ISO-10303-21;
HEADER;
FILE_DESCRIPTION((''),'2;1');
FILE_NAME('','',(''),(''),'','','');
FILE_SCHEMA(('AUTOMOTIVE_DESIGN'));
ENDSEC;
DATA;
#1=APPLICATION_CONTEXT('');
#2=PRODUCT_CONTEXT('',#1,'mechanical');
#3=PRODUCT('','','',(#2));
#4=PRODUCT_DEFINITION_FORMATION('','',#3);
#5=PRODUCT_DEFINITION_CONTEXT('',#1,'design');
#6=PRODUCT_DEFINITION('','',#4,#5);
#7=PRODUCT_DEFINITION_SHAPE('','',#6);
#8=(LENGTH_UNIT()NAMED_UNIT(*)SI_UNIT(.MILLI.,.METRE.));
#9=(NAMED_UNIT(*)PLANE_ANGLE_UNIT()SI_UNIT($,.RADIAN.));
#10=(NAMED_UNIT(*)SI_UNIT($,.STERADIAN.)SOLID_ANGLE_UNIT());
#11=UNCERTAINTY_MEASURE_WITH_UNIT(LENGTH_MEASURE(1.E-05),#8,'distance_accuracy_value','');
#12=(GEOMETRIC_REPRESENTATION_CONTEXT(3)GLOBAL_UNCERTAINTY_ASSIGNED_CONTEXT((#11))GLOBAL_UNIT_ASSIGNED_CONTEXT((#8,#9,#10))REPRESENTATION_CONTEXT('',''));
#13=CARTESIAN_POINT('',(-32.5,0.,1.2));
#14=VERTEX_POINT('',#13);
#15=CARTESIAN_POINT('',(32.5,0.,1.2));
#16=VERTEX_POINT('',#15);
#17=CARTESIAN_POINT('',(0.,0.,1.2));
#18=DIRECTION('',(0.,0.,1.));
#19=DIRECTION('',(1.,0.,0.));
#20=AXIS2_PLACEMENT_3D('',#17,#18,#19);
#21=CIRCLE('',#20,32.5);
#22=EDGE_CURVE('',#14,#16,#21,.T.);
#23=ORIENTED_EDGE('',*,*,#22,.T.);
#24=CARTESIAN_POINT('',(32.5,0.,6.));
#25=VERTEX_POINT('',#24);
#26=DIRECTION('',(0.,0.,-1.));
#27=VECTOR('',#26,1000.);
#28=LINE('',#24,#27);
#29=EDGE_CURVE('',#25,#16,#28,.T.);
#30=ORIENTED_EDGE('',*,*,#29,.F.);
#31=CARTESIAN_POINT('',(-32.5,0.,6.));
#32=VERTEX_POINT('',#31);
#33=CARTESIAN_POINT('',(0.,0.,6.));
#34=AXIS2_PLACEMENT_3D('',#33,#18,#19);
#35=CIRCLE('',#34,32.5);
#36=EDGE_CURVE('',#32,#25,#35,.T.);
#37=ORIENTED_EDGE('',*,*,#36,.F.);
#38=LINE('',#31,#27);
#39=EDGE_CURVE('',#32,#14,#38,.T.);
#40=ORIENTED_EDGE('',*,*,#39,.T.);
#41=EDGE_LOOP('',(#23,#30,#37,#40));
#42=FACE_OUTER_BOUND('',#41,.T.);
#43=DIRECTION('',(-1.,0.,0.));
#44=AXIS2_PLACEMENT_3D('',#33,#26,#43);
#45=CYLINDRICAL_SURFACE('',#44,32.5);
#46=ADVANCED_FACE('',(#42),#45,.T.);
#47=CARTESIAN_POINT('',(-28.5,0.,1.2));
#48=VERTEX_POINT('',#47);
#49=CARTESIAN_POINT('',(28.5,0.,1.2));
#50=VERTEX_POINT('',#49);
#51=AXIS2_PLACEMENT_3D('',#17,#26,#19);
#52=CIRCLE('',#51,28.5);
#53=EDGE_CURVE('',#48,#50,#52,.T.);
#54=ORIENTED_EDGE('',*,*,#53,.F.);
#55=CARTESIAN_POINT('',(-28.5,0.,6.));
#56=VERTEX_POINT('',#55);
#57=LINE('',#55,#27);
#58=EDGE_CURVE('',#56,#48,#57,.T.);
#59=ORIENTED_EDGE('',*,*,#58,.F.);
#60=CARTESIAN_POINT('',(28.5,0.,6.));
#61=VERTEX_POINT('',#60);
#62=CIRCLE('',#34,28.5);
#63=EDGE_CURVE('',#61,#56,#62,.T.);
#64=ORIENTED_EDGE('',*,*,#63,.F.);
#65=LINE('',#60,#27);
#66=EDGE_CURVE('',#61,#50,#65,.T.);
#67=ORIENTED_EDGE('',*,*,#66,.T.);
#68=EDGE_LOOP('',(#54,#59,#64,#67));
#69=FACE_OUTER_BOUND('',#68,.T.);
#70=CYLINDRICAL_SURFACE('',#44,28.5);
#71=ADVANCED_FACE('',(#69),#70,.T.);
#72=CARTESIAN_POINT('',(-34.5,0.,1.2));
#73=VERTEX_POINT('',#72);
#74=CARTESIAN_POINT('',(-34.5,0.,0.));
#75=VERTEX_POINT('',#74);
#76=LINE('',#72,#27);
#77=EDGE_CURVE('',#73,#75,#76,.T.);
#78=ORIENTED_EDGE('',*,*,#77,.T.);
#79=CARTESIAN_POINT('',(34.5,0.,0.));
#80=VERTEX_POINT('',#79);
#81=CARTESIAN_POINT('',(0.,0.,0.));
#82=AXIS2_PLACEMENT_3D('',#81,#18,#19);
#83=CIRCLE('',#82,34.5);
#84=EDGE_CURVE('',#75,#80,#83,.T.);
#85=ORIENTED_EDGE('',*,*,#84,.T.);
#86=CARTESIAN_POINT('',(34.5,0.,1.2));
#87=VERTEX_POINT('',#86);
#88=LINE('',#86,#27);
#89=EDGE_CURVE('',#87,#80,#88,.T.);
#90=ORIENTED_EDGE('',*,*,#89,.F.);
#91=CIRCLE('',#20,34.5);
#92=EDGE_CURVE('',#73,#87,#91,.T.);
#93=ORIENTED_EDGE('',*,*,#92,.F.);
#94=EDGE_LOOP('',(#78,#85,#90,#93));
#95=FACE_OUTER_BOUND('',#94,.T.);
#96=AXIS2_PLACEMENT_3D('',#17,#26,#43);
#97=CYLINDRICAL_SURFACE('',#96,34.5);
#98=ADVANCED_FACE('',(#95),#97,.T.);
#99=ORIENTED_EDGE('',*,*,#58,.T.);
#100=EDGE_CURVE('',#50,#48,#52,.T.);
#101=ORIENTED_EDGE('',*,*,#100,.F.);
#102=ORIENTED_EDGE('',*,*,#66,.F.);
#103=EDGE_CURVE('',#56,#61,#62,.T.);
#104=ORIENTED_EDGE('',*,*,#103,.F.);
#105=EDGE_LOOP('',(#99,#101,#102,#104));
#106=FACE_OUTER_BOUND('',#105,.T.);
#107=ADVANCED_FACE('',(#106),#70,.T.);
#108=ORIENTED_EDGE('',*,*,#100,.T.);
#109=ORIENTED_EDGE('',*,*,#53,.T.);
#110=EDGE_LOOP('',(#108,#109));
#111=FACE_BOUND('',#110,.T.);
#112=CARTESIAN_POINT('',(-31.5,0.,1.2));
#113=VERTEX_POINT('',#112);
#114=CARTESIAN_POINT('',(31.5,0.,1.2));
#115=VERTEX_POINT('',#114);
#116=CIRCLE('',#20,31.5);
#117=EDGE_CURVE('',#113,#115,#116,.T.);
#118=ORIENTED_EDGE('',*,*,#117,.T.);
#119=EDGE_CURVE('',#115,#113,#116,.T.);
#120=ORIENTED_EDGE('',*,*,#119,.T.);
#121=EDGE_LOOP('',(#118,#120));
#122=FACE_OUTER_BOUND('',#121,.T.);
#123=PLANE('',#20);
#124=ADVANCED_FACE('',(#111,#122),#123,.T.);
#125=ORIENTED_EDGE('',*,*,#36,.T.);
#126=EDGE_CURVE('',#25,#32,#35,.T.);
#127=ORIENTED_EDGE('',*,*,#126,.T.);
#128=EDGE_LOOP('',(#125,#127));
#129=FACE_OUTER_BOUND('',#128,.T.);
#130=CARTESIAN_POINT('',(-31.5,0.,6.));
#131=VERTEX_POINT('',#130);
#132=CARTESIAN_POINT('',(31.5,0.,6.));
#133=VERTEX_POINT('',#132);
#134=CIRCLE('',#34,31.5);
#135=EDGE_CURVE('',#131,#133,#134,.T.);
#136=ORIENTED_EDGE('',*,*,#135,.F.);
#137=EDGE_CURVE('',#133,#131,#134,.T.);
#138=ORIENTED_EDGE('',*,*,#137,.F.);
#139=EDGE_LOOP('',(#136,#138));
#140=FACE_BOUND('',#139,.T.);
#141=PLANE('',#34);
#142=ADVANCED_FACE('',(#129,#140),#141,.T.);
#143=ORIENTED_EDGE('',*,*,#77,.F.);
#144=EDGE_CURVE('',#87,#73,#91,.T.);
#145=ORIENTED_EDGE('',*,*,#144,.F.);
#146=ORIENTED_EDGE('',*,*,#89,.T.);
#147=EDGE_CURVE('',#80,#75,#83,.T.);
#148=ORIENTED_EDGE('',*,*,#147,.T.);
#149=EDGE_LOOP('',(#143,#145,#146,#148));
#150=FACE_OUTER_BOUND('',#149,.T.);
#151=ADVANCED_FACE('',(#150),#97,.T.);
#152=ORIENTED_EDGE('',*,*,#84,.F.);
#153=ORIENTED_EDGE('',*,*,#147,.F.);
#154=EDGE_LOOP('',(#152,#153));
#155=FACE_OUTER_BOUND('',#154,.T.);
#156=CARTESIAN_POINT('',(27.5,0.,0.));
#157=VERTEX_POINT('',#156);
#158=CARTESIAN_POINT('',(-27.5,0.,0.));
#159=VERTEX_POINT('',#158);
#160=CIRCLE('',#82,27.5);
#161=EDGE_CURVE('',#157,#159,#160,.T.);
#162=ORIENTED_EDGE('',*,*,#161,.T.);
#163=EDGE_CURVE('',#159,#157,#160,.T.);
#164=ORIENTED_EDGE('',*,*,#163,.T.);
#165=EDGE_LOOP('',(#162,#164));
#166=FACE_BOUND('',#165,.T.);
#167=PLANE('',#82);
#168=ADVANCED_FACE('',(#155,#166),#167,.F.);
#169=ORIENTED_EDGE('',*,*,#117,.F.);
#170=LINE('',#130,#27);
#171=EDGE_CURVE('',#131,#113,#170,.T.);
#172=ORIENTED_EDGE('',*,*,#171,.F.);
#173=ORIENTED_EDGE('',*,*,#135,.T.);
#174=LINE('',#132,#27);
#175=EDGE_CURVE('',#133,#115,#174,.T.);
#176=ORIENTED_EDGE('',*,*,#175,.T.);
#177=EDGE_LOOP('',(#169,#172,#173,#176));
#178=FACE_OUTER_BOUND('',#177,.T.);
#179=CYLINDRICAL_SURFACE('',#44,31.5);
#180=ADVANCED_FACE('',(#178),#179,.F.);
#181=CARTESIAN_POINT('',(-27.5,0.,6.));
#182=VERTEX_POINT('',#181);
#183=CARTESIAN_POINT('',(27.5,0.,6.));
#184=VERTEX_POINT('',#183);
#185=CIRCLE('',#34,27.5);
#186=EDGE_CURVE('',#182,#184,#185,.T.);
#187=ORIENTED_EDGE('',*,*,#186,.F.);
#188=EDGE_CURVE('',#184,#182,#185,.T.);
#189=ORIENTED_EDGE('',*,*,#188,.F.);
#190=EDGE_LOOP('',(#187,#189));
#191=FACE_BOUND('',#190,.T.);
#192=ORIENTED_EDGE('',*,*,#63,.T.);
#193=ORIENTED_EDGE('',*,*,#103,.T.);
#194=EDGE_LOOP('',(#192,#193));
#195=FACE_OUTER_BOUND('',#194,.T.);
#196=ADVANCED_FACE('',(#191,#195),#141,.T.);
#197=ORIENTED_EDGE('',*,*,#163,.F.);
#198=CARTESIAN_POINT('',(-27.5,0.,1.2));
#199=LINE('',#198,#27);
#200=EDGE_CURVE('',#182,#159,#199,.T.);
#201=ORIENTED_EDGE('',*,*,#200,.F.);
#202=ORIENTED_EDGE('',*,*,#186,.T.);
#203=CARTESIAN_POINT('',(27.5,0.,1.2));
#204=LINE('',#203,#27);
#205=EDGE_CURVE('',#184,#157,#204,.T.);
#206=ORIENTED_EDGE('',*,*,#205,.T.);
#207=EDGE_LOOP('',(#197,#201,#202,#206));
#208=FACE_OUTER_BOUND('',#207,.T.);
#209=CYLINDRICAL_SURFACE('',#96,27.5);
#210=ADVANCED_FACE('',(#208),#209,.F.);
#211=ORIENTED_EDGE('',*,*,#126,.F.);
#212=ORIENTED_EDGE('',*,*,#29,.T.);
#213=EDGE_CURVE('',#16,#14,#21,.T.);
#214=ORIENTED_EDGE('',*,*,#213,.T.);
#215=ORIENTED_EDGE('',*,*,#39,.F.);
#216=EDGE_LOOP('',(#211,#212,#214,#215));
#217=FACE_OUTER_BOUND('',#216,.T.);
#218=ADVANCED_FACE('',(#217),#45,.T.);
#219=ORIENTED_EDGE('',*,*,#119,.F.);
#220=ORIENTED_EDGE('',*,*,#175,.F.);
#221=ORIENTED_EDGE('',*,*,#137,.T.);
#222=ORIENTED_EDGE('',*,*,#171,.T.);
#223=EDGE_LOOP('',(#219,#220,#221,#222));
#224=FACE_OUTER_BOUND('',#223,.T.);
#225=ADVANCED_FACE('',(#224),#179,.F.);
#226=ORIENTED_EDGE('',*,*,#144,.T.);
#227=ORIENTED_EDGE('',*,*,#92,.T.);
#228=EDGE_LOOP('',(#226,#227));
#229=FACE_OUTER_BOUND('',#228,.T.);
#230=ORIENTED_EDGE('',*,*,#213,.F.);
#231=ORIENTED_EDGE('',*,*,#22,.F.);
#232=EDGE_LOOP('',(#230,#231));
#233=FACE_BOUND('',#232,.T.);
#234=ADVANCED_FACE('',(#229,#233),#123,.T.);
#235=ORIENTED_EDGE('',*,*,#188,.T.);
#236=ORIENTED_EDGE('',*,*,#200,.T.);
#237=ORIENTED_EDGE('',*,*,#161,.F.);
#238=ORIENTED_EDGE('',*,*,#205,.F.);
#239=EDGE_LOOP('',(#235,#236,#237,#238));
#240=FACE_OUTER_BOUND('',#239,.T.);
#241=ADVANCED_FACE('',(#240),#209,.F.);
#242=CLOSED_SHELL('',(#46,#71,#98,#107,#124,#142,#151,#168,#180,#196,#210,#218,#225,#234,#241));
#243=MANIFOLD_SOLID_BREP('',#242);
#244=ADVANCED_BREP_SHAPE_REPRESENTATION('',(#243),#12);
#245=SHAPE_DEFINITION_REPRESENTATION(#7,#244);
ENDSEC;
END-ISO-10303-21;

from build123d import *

# Parameters (mm, degrees)
SKETCH1_R             = 32.5
SKETCH1_R_2           = 31.5
BOSS_EXTRUDE1_DEPTH   = 6
SKETCH1_R_3           = 28.5
SKETCH1_R_4           = 27.5
BOSS_EXTRUDE1_2_DEPTH = 6
SKETCH2_R             = 34.5
SKETCH2_R_2           = 27.5
BOSS_EXTRUDE2_DEPTH   = 1.2


with BuildPart() as part:
    # Sketch1 → Boss-Extrude1 (new body)
    with BuildSketch(Plane.XY):
        Circle(SKETCH1_R)
        Circle(SKETCH1_R_2, mode=Mode.SUBTRACT)
    extrude(amount=BOSS_EXTRUDE1_DEPTH)



with BuildPart() as body_2:
    # Sketch1 → Boss-Extrude1 2 (new body)
    with BuildSketch(Plane.XY):
        Circle(SKETCH1_R_3)
        Circle(SKETCH1_R_4, mode=Mode.SUBTRACT)
    extrude(amount=BOSS_EXTRUDE1_2_DEPTH)


with BuildPart() as part_1:
    add(part.part)

    add(body_2.part)  # Boss-Extrude2 merges body 2
    # Sketch2 → Boss-Extrude2 (add)
    with BuildSketch(Plane.XY):
        Circle(SKETCH2_R)
        Circle(SKETCH2_R_2, mode=Mode.SUBTRACT)
    extrude(amount=BOSS_EXTRUDE2_DEPTH)


solid = part_1.part
